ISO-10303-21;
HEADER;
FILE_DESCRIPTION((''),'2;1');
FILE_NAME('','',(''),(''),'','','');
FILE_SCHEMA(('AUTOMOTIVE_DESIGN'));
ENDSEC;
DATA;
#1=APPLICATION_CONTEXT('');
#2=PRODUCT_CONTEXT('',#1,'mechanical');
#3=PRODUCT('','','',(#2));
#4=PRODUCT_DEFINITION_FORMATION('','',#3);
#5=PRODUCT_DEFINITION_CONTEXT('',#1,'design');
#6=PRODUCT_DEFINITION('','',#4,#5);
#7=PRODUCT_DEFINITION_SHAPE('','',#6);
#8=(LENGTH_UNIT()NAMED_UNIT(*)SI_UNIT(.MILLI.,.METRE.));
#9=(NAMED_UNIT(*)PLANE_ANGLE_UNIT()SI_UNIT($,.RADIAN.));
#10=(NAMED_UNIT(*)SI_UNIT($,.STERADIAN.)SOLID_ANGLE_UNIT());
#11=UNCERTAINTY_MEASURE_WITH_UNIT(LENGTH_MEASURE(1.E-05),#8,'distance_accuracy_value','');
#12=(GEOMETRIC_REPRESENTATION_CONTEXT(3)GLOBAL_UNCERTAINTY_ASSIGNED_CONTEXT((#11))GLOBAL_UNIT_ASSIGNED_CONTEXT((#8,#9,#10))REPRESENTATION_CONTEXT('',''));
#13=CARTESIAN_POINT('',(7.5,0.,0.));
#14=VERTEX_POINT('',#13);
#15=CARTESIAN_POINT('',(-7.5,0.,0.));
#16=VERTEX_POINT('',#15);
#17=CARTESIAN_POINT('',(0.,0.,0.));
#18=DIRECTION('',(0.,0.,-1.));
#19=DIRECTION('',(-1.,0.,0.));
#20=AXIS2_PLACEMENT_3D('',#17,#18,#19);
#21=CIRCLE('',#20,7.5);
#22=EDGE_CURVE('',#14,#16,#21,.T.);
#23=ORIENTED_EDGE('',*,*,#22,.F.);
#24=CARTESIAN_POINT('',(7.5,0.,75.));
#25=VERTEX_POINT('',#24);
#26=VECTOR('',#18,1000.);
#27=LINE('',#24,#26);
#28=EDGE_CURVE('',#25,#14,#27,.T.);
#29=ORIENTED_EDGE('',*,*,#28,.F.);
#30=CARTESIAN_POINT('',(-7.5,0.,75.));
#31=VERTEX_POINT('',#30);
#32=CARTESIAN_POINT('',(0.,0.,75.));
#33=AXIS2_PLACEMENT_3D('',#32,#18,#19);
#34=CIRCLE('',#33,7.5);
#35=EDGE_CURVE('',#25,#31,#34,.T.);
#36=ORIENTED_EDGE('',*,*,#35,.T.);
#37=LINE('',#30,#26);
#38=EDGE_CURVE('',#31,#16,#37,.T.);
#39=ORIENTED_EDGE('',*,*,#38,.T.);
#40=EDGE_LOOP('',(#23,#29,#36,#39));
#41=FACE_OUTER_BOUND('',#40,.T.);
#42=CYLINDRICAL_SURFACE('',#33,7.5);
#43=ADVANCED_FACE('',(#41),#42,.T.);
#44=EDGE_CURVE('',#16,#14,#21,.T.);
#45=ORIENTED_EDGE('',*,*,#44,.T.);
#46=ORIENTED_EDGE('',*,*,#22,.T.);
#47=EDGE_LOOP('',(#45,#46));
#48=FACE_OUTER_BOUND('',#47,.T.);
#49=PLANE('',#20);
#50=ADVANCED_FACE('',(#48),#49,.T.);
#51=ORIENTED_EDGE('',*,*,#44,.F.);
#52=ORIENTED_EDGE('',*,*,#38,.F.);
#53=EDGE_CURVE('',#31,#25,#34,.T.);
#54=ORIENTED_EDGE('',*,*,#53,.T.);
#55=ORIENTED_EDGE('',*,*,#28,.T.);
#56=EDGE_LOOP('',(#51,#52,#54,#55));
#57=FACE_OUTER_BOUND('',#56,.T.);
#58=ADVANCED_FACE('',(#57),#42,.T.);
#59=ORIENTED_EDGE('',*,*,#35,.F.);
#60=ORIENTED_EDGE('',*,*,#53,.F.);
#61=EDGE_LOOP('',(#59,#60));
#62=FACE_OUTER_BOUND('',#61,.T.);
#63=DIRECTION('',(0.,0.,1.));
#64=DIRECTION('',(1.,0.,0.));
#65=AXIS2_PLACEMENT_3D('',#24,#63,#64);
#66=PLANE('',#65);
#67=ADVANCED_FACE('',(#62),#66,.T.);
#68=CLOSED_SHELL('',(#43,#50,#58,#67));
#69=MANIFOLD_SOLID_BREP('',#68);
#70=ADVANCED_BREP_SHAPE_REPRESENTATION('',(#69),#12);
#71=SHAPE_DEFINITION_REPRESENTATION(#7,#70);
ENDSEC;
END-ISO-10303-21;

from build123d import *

# Parameters (mm, degrees)
SKETCH1_W = 7.5
SKETCH1_H = 75


with BuildPart() as part:
    # Sketch1 → Revolve1 (revolve)
    with BuildSketch(Plane.XZ, mode=Mode.PRIVATE) as revolve1_sk:
        with Locations((3.75, 37.5)):
            Rectangle(SKETCH1_W, SKETCH1_H)
    revolve(revolve1_sk.sketch.rotate(Axis((0, 0, 75), (0, 0, -1)), 180), axis=Axis((0, 0, 75), (0, 0, -1)))


solid = part.part
